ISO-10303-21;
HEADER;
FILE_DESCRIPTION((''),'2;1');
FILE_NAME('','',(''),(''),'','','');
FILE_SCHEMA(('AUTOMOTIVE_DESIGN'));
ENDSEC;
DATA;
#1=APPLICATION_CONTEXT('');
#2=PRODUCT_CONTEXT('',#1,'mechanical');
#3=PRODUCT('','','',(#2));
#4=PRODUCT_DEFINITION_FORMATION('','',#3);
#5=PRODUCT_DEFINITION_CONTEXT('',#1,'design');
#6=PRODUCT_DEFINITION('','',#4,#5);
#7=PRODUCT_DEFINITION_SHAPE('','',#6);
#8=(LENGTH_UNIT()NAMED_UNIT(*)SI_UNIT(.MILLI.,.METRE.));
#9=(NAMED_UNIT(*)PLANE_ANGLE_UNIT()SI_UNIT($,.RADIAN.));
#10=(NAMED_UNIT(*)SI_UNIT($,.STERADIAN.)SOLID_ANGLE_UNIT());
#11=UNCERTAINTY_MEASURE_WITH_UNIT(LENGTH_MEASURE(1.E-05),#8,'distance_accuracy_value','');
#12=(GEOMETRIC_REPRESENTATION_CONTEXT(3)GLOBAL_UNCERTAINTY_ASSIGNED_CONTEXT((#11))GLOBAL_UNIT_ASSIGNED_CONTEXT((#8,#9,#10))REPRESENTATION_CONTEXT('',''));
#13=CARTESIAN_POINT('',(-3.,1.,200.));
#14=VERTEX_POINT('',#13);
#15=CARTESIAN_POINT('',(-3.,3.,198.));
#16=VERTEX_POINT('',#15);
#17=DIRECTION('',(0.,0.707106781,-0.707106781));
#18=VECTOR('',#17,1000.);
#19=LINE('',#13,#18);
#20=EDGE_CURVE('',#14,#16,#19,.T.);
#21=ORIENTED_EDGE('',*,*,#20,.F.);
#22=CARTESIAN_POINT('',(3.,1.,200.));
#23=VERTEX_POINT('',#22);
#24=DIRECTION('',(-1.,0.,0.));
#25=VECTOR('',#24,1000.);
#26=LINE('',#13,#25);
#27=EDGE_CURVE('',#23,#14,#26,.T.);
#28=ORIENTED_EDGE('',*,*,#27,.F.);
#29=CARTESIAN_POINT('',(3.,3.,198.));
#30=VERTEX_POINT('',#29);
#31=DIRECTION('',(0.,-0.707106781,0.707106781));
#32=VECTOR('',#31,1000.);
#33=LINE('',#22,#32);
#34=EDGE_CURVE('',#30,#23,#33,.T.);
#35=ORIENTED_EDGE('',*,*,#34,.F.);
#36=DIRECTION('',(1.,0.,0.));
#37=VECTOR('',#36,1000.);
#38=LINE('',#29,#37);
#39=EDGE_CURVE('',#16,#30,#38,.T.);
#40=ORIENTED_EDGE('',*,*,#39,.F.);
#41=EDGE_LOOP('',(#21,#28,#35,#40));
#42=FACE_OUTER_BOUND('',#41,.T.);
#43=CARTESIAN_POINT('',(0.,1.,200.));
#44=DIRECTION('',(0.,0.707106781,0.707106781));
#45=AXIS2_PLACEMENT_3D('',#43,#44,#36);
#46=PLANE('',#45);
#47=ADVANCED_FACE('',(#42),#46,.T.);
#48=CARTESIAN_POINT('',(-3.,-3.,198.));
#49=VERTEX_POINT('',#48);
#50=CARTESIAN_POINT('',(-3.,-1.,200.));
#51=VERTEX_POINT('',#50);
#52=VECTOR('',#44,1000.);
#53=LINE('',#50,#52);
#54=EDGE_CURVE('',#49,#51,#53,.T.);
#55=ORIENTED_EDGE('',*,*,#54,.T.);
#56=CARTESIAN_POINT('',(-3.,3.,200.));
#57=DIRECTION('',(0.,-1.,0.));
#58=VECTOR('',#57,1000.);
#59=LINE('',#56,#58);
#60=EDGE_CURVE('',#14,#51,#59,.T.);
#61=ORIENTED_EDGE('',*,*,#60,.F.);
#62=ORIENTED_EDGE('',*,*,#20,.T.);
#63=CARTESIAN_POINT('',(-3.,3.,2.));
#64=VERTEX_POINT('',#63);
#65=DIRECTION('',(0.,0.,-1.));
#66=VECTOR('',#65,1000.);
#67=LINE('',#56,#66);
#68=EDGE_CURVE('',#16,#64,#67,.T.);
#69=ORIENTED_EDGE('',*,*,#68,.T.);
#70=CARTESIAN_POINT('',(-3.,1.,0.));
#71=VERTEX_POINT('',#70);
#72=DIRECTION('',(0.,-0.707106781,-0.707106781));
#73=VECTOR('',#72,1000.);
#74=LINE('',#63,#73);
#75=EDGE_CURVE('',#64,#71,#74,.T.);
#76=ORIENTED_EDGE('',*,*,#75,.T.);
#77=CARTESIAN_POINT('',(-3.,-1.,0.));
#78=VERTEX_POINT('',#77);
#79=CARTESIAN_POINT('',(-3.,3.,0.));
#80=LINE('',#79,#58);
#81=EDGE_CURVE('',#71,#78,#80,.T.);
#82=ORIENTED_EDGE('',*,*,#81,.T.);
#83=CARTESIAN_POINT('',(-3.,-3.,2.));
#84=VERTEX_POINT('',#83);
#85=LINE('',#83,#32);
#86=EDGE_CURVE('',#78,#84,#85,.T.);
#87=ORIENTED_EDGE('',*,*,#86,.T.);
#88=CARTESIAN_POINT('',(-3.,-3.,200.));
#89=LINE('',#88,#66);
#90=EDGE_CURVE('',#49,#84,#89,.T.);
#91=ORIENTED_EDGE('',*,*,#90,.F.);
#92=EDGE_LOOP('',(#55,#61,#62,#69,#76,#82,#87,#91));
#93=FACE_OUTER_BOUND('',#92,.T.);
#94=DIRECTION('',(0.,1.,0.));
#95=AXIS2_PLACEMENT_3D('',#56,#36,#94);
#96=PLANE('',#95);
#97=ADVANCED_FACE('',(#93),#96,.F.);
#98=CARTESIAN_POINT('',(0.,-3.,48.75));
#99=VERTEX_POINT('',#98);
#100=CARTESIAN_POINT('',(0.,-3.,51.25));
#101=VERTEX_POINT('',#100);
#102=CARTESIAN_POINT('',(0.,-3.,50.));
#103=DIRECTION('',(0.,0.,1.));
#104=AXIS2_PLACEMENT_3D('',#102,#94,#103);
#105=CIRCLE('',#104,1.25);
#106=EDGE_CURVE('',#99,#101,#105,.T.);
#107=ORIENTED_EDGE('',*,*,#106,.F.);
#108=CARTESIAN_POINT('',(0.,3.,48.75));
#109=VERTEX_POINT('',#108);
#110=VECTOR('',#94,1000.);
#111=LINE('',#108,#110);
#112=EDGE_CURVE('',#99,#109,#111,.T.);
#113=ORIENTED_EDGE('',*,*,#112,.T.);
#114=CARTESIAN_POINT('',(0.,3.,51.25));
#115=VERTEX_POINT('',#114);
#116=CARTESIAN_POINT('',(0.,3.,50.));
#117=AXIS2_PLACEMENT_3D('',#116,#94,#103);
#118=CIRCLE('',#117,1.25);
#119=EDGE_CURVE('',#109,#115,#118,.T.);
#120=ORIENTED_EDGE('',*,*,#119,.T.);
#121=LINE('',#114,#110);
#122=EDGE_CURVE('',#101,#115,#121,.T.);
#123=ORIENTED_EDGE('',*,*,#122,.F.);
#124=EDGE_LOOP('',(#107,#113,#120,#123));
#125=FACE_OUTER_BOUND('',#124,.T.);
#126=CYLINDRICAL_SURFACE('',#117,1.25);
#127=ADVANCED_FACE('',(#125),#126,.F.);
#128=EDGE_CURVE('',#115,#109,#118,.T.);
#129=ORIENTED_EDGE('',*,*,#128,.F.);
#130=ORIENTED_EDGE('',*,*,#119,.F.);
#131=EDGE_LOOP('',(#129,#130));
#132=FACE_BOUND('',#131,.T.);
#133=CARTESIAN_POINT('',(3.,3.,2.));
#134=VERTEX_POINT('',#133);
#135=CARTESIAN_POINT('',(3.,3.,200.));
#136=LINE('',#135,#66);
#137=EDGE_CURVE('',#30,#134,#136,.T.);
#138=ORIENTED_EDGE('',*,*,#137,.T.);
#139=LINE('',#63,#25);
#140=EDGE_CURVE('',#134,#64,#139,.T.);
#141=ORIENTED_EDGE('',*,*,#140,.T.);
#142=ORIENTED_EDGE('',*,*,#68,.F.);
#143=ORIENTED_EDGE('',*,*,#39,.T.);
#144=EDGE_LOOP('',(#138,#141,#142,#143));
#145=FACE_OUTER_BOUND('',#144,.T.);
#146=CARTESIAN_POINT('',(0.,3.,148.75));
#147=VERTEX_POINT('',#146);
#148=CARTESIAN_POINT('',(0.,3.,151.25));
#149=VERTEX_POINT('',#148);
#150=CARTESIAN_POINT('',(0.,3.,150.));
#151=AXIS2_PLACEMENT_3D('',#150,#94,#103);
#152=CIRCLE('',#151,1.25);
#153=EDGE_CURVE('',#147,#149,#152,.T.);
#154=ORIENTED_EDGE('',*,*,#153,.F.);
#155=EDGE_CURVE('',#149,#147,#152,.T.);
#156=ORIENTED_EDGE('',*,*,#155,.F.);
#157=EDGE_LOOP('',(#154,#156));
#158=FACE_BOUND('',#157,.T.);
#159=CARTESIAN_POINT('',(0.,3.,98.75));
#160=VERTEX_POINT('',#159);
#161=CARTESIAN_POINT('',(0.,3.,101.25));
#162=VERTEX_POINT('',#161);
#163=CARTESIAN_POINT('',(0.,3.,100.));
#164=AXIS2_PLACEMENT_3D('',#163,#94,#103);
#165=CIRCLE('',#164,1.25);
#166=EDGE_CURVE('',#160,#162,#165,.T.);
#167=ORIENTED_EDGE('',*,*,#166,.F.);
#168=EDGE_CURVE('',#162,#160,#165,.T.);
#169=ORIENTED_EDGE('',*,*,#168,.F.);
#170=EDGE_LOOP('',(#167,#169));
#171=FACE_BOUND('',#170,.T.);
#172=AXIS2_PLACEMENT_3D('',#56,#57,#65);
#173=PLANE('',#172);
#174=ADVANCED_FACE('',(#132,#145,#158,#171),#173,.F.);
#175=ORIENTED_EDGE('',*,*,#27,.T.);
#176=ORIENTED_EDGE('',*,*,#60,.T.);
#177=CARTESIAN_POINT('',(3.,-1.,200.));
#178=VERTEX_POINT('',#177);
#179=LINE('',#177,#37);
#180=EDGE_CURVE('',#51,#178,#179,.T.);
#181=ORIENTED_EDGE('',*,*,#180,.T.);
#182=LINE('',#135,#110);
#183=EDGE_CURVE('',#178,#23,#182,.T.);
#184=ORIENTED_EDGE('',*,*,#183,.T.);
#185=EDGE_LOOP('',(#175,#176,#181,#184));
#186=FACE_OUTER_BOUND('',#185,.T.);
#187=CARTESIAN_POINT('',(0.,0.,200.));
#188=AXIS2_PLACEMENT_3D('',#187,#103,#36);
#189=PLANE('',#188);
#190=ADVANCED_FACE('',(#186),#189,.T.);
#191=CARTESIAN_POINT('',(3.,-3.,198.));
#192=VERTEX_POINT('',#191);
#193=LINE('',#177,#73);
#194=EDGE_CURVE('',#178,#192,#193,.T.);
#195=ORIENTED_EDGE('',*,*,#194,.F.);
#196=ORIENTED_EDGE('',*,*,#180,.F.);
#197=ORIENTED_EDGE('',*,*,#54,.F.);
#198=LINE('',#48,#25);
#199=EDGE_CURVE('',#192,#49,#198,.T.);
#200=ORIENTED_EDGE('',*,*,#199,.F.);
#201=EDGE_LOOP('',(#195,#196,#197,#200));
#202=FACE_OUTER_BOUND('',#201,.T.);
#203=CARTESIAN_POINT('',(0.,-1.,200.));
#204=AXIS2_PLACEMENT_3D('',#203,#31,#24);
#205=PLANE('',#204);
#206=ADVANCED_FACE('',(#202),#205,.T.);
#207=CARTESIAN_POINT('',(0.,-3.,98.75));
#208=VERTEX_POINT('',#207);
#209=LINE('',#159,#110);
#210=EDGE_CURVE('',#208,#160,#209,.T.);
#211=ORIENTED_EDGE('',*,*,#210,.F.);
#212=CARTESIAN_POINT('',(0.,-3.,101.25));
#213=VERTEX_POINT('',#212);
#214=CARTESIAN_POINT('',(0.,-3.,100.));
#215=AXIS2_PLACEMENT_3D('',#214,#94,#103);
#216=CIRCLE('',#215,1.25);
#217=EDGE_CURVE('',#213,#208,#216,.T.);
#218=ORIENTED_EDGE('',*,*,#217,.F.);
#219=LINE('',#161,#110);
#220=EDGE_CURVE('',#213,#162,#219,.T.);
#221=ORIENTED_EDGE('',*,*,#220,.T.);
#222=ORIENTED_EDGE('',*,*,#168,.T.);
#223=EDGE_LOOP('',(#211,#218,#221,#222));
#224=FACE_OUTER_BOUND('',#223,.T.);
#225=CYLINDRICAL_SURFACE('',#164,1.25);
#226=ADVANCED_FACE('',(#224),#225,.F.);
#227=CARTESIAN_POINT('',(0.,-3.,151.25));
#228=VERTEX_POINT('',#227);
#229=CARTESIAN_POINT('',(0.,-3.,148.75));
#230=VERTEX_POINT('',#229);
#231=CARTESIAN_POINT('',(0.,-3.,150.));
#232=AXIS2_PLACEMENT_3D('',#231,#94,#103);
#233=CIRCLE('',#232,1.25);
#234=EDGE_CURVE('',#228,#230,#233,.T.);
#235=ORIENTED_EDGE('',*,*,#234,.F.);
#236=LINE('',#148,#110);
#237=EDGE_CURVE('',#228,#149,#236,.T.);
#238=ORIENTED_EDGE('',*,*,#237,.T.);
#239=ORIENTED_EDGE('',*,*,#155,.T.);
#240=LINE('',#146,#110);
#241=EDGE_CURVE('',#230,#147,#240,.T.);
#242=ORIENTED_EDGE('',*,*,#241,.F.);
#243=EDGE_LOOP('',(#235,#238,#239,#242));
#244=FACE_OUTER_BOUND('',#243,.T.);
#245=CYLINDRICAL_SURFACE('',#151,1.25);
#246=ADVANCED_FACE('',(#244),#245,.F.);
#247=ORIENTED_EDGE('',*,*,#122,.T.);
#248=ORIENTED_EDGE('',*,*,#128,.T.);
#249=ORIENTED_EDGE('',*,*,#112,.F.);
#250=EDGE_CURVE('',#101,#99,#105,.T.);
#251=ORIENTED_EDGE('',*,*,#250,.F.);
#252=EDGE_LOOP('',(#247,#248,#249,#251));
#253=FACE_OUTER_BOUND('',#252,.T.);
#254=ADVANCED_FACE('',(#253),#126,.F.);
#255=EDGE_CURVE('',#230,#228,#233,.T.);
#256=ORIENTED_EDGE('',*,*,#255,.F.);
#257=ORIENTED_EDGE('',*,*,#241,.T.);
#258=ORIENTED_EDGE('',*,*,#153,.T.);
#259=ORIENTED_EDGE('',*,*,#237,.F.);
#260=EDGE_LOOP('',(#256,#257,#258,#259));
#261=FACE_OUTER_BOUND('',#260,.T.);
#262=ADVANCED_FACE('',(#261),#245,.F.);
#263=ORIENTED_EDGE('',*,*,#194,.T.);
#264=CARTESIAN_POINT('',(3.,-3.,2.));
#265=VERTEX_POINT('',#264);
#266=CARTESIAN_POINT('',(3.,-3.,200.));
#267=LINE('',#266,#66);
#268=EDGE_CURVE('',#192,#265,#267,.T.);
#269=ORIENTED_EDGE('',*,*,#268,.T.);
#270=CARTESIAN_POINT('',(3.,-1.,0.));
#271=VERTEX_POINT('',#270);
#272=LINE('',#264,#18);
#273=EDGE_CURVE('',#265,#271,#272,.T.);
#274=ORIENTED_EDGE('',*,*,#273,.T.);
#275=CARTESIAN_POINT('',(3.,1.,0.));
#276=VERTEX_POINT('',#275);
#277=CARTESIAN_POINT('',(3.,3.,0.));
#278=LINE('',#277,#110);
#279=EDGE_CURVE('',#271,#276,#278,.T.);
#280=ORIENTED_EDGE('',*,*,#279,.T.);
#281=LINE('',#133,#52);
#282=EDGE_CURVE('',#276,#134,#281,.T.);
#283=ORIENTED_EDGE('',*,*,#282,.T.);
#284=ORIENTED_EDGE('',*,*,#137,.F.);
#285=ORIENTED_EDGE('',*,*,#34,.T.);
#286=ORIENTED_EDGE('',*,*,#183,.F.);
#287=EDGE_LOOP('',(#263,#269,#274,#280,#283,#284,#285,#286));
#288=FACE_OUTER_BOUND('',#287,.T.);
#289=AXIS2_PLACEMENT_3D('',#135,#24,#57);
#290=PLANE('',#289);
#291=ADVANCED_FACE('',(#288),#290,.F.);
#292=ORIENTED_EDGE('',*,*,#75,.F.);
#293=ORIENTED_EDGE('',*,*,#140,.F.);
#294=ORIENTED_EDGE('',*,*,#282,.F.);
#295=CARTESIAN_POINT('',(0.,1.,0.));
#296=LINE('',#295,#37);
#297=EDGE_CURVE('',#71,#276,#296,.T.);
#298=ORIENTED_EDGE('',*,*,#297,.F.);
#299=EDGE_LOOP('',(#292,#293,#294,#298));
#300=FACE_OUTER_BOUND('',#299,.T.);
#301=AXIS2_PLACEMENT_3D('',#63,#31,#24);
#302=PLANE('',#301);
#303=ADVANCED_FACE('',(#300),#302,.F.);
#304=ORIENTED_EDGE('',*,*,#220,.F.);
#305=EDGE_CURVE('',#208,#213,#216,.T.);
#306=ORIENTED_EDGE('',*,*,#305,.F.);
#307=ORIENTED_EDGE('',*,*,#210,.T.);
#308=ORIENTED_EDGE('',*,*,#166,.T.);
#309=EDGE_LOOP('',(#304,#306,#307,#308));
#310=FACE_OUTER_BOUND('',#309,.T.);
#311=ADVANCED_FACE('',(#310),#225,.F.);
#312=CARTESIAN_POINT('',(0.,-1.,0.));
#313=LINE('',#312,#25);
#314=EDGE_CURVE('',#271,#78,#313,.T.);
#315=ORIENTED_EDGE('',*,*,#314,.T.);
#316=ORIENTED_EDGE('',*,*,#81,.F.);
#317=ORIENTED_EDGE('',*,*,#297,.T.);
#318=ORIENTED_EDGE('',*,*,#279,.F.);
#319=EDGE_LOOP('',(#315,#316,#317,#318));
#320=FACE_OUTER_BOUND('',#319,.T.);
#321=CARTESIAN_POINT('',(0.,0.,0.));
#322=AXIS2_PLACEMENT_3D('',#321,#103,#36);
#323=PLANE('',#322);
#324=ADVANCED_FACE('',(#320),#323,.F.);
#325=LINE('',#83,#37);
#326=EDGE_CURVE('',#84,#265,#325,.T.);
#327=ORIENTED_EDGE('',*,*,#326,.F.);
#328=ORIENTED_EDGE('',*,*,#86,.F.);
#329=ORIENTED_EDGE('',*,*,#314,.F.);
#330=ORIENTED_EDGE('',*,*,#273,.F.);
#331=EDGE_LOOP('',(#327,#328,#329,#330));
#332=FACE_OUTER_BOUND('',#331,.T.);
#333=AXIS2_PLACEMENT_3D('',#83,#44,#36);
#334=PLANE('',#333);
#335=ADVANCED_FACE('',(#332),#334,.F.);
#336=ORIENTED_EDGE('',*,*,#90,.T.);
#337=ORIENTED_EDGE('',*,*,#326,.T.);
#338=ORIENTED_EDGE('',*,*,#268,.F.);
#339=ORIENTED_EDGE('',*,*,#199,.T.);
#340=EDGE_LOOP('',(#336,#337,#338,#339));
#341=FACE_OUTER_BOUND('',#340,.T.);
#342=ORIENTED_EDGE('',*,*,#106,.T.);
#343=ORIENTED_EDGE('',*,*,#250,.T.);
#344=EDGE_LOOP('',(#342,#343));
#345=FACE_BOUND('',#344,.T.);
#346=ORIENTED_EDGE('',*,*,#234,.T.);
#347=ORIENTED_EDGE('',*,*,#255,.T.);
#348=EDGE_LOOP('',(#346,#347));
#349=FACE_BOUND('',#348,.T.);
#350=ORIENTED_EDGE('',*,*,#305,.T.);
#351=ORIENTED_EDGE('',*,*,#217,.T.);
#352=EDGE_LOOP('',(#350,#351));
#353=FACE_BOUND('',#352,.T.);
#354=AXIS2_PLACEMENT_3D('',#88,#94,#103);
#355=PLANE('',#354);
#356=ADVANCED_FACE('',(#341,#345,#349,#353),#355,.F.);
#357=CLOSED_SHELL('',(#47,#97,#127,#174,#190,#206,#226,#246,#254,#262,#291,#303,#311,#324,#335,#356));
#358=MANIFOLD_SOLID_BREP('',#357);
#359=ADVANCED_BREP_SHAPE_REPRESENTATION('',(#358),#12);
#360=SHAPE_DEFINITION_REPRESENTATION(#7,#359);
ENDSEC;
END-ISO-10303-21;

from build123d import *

# Parameters (mm, degrees)
SKETCH_1_W         = 6
SKETCH_1_H         = 6
EXTRUDE_1_DEPTH    = 200
HOLE_WIZARD_M3_1_D = 2.5
CHAMFER_1_SIZE     = 2


with BuildPart() as part:
    # 草图1 → 凸台-拉伸1 (new body)
    with BuildSketch(Plane.XY):
        Rectangle(SKETCH_1_W, SKETCH_1_H)
    extrude(amount=EXTRUDE_1_DEPTH)

    # M3 螺纹孔1 (through all)
    with Locations(Plane(origin=(0, 3, 50), x_dir=(0, 0, 1), z_dir=(0, 1, 0))):
        with Locations((0, 0), (50, 0), (100, 0)):
            Hole(HOLE_WIZARD_M3_1_D / 2)

    # 倒角1
    chamfer_1_edges = [part.edges().sort_by_distance(p)[0] for p in [
        (0, -3, 200),
        (0, -3, 0),
        (0, 3, 0),
        (0, 3, 200),
    ]]
    chamfer(chamfer_1_edges, length=CHAMFER_1_SIZE)


solid = part.part
